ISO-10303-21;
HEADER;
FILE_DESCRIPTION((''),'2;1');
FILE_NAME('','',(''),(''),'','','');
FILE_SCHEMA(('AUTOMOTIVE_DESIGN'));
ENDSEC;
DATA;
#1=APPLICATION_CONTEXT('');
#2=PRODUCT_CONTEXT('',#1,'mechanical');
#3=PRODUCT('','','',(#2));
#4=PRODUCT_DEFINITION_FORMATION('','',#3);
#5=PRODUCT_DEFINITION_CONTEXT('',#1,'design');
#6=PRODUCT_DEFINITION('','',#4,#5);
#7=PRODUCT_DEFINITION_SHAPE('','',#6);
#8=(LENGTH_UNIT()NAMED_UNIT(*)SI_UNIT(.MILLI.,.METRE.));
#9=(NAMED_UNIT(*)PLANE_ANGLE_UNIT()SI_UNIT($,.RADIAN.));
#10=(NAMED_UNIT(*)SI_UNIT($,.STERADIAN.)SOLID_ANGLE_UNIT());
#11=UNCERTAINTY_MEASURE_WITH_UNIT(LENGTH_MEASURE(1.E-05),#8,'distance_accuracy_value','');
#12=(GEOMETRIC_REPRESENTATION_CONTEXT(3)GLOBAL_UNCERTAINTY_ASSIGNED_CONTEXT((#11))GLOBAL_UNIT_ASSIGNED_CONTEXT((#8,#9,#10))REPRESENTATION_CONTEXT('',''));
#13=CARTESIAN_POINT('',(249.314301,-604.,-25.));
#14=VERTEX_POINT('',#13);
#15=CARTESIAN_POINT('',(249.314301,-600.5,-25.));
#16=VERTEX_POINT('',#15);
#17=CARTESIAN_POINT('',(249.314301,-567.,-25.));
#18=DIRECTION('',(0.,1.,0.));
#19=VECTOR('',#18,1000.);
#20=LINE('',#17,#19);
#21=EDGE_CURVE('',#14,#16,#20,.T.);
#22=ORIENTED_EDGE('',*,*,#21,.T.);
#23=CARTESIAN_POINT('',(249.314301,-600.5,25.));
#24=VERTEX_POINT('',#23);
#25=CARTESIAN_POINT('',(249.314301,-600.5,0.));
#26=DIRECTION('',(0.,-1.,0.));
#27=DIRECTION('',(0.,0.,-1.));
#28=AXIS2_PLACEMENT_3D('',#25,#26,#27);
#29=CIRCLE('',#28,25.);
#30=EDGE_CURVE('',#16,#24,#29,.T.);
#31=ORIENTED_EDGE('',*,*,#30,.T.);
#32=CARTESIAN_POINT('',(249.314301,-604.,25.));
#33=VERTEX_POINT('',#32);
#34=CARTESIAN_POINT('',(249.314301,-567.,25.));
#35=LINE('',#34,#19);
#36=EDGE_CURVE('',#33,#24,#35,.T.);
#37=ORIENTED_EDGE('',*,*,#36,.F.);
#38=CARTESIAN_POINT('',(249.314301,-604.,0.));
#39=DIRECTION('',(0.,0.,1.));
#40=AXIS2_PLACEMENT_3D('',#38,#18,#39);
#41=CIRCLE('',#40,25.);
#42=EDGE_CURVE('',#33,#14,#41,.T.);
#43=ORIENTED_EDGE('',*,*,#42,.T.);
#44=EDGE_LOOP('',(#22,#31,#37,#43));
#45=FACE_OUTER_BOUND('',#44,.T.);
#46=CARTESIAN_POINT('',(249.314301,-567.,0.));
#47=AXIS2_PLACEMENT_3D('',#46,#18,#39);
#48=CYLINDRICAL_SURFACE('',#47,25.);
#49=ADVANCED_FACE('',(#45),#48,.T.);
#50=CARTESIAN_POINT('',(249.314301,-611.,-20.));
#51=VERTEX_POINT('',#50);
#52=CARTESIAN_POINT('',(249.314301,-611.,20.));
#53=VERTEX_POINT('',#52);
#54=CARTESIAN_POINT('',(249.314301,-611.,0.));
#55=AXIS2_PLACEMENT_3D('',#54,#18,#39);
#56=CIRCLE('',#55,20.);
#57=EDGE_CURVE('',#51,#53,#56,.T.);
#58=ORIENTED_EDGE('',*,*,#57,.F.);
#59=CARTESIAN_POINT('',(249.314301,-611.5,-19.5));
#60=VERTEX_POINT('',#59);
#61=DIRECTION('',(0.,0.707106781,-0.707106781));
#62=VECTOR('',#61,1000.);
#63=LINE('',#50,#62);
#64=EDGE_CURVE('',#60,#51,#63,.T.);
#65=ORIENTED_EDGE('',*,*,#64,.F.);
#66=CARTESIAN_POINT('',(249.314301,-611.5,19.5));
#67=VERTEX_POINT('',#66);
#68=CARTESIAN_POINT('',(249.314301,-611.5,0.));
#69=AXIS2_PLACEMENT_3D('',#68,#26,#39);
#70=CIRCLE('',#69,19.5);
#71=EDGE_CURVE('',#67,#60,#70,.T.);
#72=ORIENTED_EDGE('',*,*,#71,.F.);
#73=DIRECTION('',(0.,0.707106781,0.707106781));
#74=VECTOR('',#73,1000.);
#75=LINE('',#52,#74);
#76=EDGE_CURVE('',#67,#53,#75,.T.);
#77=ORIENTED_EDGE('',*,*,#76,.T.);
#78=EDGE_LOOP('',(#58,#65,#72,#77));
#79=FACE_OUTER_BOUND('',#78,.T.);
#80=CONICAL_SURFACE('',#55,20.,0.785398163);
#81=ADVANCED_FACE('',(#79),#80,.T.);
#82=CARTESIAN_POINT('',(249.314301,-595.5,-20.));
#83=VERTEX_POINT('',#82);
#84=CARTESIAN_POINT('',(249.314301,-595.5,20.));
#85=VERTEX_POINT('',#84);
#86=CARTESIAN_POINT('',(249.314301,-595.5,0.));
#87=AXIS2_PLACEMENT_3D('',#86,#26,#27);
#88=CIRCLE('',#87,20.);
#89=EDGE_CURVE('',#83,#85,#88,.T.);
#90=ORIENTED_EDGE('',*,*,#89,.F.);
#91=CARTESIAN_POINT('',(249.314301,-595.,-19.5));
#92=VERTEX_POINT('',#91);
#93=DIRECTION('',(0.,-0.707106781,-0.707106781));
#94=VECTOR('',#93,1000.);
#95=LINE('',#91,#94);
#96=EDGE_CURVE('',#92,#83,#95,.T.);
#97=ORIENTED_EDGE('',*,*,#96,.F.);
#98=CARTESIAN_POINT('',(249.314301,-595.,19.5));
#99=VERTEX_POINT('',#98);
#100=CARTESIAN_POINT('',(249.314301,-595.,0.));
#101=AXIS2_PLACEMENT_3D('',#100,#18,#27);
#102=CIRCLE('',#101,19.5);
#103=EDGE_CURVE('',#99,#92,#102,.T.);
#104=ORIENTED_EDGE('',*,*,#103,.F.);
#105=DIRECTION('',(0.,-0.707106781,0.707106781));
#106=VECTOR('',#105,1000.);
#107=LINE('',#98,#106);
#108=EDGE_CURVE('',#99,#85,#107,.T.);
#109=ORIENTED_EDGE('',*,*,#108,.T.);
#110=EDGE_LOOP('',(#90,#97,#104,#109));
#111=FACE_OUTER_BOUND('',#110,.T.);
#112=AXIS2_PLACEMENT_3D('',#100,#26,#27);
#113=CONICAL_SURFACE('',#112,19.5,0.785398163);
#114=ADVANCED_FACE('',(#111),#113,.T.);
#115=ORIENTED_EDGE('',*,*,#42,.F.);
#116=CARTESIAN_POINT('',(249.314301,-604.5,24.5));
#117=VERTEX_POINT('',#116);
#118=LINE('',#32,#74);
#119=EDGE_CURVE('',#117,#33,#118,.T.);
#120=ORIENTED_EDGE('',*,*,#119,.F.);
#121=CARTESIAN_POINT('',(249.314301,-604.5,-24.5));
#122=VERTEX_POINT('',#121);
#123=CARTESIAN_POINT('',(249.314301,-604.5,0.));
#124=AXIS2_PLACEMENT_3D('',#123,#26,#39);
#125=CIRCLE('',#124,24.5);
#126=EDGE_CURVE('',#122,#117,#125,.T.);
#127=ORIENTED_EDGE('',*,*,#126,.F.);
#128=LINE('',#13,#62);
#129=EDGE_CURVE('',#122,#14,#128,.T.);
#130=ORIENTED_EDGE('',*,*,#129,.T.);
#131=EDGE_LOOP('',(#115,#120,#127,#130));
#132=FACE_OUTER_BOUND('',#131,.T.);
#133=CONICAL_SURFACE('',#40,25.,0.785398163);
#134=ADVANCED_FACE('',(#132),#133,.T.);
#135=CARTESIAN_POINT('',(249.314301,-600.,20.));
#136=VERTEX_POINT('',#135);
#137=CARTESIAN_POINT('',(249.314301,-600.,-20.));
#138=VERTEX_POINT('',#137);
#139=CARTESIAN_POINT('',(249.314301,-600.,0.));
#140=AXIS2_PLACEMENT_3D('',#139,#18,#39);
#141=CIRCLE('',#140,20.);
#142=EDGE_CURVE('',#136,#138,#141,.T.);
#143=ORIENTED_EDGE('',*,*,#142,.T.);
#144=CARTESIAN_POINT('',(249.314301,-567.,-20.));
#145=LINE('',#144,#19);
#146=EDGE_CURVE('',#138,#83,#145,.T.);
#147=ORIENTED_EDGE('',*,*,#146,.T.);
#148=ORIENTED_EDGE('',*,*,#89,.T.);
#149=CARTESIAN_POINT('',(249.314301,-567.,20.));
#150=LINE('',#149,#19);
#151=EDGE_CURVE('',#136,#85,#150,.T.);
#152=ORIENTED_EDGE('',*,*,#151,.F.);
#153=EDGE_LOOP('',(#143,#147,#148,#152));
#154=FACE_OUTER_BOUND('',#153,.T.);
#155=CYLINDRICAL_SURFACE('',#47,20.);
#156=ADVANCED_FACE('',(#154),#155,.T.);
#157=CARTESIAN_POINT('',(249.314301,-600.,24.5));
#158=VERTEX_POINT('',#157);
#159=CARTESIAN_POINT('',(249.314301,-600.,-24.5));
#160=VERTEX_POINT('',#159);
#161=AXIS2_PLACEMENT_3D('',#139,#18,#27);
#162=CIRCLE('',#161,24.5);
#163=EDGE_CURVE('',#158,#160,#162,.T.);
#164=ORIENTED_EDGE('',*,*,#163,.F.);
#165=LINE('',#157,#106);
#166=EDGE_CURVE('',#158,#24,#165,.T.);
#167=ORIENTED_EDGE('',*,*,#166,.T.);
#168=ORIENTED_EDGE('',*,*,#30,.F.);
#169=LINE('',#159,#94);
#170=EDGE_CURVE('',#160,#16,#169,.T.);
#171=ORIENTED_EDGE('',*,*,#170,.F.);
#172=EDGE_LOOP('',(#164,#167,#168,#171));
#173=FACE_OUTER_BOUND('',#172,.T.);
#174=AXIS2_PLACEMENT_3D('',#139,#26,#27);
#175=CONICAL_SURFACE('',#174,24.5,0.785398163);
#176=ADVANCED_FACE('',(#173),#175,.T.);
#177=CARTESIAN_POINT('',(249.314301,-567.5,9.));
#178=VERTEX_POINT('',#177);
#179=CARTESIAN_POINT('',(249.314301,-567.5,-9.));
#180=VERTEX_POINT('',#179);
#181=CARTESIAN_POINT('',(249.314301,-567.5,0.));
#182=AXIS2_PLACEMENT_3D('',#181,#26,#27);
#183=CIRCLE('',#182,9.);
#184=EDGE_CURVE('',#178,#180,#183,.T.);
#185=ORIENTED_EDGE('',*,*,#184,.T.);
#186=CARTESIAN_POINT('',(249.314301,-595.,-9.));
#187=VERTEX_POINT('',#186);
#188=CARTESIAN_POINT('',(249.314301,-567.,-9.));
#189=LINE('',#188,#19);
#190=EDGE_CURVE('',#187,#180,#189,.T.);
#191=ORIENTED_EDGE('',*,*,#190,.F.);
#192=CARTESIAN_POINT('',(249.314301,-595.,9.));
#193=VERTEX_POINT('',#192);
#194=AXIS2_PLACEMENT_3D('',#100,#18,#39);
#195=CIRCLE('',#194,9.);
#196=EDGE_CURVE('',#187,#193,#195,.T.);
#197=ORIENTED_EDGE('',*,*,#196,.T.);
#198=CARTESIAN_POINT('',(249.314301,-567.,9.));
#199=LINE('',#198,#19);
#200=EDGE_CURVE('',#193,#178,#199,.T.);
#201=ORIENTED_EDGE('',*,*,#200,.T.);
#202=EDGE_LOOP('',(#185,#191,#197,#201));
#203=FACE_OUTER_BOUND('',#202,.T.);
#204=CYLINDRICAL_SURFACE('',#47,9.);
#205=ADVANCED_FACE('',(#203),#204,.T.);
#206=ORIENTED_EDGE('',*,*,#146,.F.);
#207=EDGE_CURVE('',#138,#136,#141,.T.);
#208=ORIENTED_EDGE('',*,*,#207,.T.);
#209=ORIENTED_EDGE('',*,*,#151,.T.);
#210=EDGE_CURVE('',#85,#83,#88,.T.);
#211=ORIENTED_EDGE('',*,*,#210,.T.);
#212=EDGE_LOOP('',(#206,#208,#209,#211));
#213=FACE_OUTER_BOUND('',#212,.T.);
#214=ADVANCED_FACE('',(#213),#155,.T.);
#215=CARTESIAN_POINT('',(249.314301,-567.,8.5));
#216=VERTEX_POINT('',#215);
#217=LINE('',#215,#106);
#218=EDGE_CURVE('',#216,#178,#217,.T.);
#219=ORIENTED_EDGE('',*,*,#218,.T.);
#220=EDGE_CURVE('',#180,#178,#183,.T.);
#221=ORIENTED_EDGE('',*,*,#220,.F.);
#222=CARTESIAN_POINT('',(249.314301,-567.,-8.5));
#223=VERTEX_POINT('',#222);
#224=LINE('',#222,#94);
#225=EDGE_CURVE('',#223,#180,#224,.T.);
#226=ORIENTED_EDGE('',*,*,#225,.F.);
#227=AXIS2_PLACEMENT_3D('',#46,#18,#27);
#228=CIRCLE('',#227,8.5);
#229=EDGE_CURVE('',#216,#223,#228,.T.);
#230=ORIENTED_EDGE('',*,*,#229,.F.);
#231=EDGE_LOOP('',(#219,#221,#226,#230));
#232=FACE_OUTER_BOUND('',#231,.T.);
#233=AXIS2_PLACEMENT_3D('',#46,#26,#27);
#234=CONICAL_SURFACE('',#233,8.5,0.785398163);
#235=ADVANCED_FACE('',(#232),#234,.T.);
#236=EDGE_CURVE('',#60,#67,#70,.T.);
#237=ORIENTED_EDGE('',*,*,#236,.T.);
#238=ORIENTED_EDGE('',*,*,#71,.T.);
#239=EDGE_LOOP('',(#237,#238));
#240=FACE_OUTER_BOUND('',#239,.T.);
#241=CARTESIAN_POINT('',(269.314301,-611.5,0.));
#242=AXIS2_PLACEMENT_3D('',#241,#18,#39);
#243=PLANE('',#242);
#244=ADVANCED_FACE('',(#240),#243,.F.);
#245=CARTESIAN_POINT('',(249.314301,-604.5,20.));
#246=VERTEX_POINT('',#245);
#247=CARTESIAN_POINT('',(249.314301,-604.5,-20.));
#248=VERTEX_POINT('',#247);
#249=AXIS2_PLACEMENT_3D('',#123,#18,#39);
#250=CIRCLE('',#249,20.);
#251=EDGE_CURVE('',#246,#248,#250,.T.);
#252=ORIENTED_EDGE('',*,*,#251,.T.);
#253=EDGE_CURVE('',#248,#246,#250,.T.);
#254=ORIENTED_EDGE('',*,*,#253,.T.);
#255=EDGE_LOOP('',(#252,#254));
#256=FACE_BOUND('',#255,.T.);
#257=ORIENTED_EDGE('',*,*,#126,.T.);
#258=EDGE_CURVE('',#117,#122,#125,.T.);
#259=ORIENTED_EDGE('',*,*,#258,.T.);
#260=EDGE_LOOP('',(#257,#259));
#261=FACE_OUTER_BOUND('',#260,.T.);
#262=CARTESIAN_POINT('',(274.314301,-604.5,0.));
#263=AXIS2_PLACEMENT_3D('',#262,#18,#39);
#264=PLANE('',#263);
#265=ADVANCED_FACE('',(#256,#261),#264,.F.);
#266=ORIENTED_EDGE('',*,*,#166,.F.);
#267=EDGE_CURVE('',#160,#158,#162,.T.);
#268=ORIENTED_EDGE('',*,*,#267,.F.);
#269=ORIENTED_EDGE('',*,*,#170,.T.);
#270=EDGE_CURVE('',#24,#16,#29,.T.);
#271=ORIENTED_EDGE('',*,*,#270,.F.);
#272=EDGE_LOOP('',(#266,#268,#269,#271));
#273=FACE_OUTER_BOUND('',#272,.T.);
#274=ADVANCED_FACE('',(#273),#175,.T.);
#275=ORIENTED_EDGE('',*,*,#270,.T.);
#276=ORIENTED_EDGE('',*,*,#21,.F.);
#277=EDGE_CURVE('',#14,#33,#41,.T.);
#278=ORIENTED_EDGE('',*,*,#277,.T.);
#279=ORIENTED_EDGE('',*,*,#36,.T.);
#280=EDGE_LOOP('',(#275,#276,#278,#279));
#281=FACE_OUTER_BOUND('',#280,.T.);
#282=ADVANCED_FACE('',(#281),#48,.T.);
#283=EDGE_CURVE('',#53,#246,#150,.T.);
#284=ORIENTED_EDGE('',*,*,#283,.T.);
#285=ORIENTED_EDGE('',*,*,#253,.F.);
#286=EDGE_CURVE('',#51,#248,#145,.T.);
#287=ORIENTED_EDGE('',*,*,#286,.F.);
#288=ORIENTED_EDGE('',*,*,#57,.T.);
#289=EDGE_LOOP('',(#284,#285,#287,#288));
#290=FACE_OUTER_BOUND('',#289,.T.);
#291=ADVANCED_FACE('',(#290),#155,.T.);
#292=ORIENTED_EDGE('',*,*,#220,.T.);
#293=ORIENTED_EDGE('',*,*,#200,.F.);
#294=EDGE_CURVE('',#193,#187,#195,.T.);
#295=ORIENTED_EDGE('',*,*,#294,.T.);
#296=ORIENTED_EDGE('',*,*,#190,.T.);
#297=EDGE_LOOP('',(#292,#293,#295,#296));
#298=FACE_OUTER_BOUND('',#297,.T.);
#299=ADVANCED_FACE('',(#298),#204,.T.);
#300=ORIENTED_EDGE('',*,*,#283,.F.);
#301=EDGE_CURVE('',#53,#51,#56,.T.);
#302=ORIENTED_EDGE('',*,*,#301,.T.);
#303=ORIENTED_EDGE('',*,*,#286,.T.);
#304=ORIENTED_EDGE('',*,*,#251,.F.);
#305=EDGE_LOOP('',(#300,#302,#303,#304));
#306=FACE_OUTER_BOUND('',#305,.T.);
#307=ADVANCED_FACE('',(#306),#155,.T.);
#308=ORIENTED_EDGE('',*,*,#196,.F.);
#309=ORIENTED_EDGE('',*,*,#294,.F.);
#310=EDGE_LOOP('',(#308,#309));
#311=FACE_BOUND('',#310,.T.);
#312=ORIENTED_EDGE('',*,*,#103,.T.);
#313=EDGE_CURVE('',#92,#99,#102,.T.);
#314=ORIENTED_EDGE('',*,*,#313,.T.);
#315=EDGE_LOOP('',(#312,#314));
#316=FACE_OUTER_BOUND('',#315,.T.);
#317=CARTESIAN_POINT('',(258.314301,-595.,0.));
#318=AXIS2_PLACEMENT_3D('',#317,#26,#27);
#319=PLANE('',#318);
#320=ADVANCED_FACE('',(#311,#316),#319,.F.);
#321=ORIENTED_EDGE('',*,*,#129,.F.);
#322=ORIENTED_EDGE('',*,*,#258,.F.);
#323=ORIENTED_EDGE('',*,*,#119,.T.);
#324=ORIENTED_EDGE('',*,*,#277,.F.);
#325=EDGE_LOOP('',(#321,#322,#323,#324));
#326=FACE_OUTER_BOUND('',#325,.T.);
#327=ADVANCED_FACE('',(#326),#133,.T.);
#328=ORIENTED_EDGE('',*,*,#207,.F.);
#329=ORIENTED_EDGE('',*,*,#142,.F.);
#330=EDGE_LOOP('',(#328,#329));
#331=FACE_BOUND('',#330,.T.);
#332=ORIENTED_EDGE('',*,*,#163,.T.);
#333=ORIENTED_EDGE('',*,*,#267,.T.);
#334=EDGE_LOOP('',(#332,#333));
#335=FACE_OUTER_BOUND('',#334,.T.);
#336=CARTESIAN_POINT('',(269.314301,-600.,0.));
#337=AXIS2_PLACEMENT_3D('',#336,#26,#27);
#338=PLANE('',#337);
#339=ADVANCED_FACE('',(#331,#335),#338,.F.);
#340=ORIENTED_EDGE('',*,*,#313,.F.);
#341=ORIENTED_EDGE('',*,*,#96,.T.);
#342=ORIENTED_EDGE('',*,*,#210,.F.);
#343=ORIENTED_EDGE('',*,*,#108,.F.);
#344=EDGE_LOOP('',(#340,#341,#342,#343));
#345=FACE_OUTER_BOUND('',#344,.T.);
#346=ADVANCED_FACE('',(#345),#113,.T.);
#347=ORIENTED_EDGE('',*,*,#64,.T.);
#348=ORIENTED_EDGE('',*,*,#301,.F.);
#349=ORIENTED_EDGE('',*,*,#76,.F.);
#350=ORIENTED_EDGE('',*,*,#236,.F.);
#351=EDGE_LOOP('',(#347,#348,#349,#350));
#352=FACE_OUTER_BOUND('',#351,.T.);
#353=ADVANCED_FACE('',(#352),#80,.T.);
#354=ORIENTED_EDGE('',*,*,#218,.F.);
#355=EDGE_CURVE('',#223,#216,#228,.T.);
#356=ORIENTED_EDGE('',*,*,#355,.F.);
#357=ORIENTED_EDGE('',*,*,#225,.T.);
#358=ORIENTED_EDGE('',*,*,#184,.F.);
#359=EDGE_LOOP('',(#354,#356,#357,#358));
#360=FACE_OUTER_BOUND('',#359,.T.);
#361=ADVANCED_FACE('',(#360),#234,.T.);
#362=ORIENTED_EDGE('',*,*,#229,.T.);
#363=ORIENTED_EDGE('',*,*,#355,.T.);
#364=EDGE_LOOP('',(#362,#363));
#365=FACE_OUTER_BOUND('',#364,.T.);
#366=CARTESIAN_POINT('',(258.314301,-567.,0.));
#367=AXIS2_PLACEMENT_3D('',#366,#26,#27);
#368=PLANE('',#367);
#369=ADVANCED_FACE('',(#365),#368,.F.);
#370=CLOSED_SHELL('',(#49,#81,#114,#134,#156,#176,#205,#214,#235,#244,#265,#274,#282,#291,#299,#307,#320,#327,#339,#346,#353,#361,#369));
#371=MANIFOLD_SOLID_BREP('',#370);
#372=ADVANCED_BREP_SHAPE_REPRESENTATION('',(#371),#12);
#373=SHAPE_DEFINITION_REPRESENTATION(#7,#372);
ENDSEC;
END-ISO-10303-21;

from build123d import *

# Parameters (mm, degrees)
CHAMFER1_SIZE = 0.5


with BuildPart() as part:
    # Sketch1 → Revolve1 (revolve)
    with BuildSketch(Plane.XY, mode=Mode.PRIVATE) as revolve1_sk:
        Polygon((258.314300847, -567), (258.314300847, -595), (269.314300847, -595), (269.314300847, -600), (274.314300847, -600), (274.314300847, -604.5), (269.314300847, -604.5), (269.314300847, -611.5), (249.314300847, -611.5), (249.314300847, -567), align=None)
    revolve(revolve1_sk.sketch.rotate(Axis((249.314300847, -567, 0), (0, -1, 0)), 90), axis=Axis((249.314300847, -567, 0), (0, -1, 0)))

    # Chamfer1
    chamfer1_edges = [part.edges().sort_by_distance(p)[0] for p in [
        (249.314300847, -604.5, -25),
        (249.314300847, -611.5, -20),
        (249.314300847, -567, -9),
        (249.314300847, -595, -20),
        (249.314300847, -600, -25),
    ]]
    chamfer(chamfer1_edges, length=CHAMFER1_SIZE)


solid = part.part
